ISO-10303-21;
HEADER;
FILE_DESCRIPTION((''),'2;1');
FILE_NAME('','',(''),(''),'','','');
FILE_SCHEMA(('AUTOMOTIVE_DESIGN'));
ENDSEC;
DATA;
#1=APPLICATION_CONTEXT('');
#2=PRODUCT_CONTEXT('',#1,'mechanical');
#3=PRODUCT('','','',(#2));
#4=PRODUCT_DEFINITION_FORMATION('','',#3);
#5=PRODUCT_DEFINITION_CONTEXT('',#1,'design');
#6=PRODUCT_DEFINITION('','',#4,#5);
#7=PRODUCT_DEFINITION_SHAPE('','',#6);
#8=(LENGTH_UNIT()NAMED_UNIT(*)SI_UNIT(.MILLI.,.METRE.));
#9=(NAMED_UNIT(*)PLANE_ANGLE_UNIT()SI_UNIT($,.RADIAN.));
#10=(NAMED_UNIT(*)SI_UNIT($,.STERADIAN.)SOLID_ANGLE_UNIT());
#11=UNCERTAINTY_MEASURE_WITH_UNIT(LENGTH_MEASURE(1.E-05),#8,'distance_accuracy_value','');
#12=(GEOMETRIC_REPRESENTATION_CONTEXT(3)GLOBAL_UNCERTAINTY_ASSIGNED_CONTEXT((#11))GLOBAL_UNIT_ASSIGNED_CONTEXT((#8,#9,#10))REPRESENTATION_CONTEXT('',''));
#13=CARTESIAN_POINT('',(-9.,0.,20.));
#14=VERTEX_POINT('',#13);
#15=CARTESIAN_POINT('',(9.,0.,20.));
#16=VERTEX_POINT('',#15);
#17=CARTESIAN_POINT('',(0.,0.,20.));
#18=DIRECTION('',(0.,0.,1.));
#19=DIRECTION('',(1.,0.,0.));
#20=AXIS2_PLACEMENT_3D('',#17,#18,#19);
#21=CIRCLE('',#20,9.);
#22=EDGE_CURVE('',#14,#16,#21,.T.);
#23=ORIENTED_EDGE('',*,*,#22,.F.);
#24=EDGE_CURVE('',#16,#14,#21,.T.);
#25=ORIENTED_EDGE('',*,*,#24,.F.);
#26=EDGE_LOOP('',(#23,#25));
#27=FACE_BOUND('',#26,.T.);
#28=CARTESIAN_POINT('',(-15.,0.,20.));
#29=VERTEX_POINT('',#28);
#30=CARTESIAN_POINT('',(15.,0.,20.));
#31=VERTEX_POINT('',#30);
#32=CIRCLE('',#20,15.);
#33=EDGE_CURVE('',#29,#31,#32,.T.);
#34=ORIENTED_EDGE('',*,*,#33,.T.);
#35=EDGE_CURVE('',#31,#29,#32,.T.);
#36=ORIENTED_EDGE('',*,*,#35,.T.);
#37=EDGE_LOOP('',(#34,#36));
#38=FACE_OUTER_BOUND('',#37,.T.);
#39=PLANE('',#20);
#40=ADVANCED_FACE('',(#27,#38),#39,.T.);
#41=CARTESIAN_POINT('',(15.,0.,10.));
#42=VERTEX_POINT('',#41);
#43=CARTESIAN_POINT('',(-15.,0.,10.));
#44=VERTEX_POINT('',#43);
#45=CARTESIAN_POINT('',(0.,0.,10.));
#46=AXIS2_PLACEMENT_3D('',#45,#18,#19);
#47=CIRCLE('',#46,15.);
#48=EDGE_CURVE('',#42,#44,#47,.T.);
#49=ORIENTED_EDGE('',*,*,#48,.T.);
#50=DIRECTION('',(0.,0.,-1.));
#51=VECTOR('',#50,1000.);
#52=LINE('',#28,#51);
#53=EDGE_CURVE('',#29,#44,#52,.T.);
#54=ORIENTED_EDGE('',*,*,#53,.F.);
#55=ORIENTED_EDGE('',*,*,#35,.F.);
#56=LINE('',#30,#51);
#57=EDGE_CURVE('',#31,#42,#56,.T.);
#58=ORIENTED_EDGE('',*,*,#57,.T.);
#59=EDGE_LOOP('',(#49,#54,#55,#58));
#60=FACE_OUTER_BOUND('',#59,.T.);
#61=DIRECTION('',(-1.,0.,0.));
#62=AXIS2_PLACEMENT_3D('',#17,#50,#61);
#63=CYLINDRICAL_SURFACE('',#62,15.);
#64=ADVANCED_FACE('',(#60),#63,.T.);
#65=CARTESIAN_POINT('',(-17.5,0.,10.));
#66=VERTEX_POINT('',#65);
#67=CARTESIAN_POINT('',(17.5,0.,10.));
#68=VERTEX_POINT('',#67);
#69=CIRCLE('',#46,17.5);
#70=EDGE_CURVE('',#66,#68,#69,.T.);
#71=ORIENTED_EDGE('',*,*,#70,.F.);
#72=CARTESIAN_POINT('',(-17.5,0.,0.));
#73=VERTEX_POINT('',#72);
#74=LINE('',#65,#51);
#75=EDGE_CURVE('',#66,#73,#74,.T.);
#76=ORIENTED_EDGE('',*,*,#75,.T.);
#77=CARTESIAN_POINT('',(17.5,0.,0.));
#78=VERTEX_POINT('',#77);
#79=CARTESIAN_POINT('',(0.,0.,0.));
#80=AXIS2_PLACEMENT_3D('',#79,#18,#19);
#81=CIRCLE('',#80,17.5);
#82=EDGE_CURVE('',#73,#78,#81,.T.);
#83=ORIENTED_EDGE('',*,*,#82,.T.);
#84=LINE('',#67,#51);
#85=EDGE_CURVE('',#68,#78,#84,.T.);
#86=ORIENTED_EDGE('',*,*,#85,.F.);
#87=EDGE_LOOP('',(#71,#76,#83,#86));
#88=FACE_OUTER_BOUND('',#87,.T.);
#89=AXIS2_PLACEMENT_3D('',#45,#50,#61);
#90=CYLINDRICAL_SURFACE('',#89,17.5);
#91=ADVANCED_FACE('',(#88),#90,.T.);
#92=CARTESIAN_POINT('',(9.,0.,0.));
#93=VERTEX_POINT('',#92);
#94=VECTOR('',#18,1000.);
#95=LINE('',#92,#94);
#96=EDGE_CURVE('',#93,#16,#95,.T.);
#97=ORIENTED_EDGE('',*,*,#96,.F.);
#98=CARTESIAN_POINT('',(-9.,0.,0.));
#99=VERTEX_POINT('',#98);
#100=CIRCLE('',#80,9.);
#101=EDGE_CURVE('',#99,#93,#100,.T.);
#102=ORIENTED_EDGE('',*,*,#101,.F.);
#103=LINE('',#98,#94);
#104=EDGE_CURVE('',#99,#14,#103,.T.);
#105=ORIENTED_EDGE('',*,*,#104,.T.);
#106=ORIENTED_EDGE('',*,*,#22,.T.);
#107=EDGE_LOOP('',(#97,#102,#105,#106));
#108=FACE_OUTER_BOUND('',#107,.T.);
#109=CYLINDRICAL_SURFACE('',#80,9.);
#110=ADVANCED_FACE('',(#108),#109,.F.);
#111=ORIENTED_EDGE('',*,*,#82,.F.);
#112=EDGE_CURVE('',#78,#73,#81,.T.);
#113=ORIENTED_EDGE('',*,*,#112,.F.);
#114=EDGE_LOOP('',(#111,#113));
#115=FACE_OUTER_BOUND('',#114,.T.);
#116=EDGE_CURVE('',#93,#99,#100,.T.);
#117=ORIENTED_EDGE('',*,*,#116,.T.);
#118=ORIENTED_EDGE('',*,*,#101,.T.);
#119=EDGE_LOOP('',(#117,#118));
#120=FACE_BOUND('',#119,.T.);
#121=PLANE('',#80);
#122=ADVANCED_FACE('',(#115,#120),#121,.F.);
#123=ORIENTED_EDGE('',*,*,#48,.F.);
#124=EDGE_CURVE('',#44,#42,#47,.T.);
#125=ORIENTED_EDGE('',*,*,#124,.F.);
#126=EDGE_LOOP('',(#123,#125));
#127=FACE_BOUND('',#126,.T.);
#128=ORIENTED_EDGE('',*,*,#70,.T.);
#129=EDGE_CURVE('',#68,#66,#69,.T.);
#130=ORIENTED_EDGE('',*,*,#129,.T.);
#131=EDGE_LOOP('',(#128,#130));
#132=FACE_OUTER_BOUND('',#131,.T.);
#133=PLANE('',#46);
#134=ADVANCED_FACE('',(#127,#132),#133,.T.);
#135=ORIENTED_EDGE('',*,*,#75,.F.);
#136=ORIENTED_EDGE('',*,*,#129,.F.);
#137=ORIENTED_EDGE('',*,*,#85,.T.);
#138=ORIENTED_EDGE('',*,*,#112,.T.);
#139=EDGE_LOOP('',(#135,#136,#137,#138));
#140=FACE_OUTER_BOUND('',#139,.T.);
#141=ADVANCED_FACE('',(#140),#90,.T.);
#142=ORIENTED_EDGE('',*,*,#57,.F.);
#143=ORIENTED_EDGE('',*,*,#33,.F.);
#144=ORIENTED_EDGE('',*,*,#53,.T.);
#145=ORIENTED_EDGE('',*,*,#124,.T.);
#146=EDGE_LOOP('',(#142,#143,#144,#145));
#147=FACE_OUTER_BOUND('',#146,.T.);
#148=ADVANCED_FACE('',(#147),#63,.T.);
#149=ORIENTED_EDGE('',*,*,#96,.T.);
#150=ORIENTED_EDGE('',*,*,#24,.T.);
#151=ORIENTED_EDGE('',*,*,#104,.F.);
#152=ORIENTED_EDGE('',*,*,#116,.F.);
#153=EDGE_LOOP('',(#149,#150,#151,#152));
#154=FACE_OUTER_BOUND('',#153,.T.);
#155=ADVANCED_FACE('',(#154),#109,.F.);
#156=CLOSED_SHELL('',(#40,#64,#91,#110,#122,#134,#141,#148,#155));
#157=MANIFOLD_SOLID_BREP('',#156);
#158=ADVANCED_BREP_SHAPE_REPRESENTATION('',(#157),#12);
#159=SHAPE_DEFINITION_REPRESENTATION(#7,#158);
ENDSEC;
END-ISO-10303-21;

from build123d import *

# Parameters (mm, degrees)
SKETCH1_R           = 17.5
BOSS_EXTRUDE1_DEPTH = 10
SKETCH3_R           = 15
BOSS_EXTRUDE2_DEPTH = 10
SKETCH4_R           = 9
CUT_EXTRUDE1_DEPTH  = 32.819805153


with BuildPart() as part:
    # Sketch1 → Boss-Extrude1 (new body)
    with BuildSketch(Plane.XY):
        Circle(SKETCH1_R)
    extrude(amount=BOSS_EXTRUDE1_DEPTH)

    # Sketch3 → Boss-Extrude2 (add)
    with BuildSketch(Plane.XY.offset(10)):
        Circle(SKETCH3_R)
    extrude(amount=BOSS_EXTRUDE2_DEPTH)

    # Sketch4 → Cut-Extrude1 (cut, through all)
    with BuildSketch(Plane.XY.offset(20)):
        Circle(SKETCH4_R)
    extrude(amount=-CUT_EXTRUDE1_DEPTH, mode=Mode.SUBTRACT)


solid = part.part
